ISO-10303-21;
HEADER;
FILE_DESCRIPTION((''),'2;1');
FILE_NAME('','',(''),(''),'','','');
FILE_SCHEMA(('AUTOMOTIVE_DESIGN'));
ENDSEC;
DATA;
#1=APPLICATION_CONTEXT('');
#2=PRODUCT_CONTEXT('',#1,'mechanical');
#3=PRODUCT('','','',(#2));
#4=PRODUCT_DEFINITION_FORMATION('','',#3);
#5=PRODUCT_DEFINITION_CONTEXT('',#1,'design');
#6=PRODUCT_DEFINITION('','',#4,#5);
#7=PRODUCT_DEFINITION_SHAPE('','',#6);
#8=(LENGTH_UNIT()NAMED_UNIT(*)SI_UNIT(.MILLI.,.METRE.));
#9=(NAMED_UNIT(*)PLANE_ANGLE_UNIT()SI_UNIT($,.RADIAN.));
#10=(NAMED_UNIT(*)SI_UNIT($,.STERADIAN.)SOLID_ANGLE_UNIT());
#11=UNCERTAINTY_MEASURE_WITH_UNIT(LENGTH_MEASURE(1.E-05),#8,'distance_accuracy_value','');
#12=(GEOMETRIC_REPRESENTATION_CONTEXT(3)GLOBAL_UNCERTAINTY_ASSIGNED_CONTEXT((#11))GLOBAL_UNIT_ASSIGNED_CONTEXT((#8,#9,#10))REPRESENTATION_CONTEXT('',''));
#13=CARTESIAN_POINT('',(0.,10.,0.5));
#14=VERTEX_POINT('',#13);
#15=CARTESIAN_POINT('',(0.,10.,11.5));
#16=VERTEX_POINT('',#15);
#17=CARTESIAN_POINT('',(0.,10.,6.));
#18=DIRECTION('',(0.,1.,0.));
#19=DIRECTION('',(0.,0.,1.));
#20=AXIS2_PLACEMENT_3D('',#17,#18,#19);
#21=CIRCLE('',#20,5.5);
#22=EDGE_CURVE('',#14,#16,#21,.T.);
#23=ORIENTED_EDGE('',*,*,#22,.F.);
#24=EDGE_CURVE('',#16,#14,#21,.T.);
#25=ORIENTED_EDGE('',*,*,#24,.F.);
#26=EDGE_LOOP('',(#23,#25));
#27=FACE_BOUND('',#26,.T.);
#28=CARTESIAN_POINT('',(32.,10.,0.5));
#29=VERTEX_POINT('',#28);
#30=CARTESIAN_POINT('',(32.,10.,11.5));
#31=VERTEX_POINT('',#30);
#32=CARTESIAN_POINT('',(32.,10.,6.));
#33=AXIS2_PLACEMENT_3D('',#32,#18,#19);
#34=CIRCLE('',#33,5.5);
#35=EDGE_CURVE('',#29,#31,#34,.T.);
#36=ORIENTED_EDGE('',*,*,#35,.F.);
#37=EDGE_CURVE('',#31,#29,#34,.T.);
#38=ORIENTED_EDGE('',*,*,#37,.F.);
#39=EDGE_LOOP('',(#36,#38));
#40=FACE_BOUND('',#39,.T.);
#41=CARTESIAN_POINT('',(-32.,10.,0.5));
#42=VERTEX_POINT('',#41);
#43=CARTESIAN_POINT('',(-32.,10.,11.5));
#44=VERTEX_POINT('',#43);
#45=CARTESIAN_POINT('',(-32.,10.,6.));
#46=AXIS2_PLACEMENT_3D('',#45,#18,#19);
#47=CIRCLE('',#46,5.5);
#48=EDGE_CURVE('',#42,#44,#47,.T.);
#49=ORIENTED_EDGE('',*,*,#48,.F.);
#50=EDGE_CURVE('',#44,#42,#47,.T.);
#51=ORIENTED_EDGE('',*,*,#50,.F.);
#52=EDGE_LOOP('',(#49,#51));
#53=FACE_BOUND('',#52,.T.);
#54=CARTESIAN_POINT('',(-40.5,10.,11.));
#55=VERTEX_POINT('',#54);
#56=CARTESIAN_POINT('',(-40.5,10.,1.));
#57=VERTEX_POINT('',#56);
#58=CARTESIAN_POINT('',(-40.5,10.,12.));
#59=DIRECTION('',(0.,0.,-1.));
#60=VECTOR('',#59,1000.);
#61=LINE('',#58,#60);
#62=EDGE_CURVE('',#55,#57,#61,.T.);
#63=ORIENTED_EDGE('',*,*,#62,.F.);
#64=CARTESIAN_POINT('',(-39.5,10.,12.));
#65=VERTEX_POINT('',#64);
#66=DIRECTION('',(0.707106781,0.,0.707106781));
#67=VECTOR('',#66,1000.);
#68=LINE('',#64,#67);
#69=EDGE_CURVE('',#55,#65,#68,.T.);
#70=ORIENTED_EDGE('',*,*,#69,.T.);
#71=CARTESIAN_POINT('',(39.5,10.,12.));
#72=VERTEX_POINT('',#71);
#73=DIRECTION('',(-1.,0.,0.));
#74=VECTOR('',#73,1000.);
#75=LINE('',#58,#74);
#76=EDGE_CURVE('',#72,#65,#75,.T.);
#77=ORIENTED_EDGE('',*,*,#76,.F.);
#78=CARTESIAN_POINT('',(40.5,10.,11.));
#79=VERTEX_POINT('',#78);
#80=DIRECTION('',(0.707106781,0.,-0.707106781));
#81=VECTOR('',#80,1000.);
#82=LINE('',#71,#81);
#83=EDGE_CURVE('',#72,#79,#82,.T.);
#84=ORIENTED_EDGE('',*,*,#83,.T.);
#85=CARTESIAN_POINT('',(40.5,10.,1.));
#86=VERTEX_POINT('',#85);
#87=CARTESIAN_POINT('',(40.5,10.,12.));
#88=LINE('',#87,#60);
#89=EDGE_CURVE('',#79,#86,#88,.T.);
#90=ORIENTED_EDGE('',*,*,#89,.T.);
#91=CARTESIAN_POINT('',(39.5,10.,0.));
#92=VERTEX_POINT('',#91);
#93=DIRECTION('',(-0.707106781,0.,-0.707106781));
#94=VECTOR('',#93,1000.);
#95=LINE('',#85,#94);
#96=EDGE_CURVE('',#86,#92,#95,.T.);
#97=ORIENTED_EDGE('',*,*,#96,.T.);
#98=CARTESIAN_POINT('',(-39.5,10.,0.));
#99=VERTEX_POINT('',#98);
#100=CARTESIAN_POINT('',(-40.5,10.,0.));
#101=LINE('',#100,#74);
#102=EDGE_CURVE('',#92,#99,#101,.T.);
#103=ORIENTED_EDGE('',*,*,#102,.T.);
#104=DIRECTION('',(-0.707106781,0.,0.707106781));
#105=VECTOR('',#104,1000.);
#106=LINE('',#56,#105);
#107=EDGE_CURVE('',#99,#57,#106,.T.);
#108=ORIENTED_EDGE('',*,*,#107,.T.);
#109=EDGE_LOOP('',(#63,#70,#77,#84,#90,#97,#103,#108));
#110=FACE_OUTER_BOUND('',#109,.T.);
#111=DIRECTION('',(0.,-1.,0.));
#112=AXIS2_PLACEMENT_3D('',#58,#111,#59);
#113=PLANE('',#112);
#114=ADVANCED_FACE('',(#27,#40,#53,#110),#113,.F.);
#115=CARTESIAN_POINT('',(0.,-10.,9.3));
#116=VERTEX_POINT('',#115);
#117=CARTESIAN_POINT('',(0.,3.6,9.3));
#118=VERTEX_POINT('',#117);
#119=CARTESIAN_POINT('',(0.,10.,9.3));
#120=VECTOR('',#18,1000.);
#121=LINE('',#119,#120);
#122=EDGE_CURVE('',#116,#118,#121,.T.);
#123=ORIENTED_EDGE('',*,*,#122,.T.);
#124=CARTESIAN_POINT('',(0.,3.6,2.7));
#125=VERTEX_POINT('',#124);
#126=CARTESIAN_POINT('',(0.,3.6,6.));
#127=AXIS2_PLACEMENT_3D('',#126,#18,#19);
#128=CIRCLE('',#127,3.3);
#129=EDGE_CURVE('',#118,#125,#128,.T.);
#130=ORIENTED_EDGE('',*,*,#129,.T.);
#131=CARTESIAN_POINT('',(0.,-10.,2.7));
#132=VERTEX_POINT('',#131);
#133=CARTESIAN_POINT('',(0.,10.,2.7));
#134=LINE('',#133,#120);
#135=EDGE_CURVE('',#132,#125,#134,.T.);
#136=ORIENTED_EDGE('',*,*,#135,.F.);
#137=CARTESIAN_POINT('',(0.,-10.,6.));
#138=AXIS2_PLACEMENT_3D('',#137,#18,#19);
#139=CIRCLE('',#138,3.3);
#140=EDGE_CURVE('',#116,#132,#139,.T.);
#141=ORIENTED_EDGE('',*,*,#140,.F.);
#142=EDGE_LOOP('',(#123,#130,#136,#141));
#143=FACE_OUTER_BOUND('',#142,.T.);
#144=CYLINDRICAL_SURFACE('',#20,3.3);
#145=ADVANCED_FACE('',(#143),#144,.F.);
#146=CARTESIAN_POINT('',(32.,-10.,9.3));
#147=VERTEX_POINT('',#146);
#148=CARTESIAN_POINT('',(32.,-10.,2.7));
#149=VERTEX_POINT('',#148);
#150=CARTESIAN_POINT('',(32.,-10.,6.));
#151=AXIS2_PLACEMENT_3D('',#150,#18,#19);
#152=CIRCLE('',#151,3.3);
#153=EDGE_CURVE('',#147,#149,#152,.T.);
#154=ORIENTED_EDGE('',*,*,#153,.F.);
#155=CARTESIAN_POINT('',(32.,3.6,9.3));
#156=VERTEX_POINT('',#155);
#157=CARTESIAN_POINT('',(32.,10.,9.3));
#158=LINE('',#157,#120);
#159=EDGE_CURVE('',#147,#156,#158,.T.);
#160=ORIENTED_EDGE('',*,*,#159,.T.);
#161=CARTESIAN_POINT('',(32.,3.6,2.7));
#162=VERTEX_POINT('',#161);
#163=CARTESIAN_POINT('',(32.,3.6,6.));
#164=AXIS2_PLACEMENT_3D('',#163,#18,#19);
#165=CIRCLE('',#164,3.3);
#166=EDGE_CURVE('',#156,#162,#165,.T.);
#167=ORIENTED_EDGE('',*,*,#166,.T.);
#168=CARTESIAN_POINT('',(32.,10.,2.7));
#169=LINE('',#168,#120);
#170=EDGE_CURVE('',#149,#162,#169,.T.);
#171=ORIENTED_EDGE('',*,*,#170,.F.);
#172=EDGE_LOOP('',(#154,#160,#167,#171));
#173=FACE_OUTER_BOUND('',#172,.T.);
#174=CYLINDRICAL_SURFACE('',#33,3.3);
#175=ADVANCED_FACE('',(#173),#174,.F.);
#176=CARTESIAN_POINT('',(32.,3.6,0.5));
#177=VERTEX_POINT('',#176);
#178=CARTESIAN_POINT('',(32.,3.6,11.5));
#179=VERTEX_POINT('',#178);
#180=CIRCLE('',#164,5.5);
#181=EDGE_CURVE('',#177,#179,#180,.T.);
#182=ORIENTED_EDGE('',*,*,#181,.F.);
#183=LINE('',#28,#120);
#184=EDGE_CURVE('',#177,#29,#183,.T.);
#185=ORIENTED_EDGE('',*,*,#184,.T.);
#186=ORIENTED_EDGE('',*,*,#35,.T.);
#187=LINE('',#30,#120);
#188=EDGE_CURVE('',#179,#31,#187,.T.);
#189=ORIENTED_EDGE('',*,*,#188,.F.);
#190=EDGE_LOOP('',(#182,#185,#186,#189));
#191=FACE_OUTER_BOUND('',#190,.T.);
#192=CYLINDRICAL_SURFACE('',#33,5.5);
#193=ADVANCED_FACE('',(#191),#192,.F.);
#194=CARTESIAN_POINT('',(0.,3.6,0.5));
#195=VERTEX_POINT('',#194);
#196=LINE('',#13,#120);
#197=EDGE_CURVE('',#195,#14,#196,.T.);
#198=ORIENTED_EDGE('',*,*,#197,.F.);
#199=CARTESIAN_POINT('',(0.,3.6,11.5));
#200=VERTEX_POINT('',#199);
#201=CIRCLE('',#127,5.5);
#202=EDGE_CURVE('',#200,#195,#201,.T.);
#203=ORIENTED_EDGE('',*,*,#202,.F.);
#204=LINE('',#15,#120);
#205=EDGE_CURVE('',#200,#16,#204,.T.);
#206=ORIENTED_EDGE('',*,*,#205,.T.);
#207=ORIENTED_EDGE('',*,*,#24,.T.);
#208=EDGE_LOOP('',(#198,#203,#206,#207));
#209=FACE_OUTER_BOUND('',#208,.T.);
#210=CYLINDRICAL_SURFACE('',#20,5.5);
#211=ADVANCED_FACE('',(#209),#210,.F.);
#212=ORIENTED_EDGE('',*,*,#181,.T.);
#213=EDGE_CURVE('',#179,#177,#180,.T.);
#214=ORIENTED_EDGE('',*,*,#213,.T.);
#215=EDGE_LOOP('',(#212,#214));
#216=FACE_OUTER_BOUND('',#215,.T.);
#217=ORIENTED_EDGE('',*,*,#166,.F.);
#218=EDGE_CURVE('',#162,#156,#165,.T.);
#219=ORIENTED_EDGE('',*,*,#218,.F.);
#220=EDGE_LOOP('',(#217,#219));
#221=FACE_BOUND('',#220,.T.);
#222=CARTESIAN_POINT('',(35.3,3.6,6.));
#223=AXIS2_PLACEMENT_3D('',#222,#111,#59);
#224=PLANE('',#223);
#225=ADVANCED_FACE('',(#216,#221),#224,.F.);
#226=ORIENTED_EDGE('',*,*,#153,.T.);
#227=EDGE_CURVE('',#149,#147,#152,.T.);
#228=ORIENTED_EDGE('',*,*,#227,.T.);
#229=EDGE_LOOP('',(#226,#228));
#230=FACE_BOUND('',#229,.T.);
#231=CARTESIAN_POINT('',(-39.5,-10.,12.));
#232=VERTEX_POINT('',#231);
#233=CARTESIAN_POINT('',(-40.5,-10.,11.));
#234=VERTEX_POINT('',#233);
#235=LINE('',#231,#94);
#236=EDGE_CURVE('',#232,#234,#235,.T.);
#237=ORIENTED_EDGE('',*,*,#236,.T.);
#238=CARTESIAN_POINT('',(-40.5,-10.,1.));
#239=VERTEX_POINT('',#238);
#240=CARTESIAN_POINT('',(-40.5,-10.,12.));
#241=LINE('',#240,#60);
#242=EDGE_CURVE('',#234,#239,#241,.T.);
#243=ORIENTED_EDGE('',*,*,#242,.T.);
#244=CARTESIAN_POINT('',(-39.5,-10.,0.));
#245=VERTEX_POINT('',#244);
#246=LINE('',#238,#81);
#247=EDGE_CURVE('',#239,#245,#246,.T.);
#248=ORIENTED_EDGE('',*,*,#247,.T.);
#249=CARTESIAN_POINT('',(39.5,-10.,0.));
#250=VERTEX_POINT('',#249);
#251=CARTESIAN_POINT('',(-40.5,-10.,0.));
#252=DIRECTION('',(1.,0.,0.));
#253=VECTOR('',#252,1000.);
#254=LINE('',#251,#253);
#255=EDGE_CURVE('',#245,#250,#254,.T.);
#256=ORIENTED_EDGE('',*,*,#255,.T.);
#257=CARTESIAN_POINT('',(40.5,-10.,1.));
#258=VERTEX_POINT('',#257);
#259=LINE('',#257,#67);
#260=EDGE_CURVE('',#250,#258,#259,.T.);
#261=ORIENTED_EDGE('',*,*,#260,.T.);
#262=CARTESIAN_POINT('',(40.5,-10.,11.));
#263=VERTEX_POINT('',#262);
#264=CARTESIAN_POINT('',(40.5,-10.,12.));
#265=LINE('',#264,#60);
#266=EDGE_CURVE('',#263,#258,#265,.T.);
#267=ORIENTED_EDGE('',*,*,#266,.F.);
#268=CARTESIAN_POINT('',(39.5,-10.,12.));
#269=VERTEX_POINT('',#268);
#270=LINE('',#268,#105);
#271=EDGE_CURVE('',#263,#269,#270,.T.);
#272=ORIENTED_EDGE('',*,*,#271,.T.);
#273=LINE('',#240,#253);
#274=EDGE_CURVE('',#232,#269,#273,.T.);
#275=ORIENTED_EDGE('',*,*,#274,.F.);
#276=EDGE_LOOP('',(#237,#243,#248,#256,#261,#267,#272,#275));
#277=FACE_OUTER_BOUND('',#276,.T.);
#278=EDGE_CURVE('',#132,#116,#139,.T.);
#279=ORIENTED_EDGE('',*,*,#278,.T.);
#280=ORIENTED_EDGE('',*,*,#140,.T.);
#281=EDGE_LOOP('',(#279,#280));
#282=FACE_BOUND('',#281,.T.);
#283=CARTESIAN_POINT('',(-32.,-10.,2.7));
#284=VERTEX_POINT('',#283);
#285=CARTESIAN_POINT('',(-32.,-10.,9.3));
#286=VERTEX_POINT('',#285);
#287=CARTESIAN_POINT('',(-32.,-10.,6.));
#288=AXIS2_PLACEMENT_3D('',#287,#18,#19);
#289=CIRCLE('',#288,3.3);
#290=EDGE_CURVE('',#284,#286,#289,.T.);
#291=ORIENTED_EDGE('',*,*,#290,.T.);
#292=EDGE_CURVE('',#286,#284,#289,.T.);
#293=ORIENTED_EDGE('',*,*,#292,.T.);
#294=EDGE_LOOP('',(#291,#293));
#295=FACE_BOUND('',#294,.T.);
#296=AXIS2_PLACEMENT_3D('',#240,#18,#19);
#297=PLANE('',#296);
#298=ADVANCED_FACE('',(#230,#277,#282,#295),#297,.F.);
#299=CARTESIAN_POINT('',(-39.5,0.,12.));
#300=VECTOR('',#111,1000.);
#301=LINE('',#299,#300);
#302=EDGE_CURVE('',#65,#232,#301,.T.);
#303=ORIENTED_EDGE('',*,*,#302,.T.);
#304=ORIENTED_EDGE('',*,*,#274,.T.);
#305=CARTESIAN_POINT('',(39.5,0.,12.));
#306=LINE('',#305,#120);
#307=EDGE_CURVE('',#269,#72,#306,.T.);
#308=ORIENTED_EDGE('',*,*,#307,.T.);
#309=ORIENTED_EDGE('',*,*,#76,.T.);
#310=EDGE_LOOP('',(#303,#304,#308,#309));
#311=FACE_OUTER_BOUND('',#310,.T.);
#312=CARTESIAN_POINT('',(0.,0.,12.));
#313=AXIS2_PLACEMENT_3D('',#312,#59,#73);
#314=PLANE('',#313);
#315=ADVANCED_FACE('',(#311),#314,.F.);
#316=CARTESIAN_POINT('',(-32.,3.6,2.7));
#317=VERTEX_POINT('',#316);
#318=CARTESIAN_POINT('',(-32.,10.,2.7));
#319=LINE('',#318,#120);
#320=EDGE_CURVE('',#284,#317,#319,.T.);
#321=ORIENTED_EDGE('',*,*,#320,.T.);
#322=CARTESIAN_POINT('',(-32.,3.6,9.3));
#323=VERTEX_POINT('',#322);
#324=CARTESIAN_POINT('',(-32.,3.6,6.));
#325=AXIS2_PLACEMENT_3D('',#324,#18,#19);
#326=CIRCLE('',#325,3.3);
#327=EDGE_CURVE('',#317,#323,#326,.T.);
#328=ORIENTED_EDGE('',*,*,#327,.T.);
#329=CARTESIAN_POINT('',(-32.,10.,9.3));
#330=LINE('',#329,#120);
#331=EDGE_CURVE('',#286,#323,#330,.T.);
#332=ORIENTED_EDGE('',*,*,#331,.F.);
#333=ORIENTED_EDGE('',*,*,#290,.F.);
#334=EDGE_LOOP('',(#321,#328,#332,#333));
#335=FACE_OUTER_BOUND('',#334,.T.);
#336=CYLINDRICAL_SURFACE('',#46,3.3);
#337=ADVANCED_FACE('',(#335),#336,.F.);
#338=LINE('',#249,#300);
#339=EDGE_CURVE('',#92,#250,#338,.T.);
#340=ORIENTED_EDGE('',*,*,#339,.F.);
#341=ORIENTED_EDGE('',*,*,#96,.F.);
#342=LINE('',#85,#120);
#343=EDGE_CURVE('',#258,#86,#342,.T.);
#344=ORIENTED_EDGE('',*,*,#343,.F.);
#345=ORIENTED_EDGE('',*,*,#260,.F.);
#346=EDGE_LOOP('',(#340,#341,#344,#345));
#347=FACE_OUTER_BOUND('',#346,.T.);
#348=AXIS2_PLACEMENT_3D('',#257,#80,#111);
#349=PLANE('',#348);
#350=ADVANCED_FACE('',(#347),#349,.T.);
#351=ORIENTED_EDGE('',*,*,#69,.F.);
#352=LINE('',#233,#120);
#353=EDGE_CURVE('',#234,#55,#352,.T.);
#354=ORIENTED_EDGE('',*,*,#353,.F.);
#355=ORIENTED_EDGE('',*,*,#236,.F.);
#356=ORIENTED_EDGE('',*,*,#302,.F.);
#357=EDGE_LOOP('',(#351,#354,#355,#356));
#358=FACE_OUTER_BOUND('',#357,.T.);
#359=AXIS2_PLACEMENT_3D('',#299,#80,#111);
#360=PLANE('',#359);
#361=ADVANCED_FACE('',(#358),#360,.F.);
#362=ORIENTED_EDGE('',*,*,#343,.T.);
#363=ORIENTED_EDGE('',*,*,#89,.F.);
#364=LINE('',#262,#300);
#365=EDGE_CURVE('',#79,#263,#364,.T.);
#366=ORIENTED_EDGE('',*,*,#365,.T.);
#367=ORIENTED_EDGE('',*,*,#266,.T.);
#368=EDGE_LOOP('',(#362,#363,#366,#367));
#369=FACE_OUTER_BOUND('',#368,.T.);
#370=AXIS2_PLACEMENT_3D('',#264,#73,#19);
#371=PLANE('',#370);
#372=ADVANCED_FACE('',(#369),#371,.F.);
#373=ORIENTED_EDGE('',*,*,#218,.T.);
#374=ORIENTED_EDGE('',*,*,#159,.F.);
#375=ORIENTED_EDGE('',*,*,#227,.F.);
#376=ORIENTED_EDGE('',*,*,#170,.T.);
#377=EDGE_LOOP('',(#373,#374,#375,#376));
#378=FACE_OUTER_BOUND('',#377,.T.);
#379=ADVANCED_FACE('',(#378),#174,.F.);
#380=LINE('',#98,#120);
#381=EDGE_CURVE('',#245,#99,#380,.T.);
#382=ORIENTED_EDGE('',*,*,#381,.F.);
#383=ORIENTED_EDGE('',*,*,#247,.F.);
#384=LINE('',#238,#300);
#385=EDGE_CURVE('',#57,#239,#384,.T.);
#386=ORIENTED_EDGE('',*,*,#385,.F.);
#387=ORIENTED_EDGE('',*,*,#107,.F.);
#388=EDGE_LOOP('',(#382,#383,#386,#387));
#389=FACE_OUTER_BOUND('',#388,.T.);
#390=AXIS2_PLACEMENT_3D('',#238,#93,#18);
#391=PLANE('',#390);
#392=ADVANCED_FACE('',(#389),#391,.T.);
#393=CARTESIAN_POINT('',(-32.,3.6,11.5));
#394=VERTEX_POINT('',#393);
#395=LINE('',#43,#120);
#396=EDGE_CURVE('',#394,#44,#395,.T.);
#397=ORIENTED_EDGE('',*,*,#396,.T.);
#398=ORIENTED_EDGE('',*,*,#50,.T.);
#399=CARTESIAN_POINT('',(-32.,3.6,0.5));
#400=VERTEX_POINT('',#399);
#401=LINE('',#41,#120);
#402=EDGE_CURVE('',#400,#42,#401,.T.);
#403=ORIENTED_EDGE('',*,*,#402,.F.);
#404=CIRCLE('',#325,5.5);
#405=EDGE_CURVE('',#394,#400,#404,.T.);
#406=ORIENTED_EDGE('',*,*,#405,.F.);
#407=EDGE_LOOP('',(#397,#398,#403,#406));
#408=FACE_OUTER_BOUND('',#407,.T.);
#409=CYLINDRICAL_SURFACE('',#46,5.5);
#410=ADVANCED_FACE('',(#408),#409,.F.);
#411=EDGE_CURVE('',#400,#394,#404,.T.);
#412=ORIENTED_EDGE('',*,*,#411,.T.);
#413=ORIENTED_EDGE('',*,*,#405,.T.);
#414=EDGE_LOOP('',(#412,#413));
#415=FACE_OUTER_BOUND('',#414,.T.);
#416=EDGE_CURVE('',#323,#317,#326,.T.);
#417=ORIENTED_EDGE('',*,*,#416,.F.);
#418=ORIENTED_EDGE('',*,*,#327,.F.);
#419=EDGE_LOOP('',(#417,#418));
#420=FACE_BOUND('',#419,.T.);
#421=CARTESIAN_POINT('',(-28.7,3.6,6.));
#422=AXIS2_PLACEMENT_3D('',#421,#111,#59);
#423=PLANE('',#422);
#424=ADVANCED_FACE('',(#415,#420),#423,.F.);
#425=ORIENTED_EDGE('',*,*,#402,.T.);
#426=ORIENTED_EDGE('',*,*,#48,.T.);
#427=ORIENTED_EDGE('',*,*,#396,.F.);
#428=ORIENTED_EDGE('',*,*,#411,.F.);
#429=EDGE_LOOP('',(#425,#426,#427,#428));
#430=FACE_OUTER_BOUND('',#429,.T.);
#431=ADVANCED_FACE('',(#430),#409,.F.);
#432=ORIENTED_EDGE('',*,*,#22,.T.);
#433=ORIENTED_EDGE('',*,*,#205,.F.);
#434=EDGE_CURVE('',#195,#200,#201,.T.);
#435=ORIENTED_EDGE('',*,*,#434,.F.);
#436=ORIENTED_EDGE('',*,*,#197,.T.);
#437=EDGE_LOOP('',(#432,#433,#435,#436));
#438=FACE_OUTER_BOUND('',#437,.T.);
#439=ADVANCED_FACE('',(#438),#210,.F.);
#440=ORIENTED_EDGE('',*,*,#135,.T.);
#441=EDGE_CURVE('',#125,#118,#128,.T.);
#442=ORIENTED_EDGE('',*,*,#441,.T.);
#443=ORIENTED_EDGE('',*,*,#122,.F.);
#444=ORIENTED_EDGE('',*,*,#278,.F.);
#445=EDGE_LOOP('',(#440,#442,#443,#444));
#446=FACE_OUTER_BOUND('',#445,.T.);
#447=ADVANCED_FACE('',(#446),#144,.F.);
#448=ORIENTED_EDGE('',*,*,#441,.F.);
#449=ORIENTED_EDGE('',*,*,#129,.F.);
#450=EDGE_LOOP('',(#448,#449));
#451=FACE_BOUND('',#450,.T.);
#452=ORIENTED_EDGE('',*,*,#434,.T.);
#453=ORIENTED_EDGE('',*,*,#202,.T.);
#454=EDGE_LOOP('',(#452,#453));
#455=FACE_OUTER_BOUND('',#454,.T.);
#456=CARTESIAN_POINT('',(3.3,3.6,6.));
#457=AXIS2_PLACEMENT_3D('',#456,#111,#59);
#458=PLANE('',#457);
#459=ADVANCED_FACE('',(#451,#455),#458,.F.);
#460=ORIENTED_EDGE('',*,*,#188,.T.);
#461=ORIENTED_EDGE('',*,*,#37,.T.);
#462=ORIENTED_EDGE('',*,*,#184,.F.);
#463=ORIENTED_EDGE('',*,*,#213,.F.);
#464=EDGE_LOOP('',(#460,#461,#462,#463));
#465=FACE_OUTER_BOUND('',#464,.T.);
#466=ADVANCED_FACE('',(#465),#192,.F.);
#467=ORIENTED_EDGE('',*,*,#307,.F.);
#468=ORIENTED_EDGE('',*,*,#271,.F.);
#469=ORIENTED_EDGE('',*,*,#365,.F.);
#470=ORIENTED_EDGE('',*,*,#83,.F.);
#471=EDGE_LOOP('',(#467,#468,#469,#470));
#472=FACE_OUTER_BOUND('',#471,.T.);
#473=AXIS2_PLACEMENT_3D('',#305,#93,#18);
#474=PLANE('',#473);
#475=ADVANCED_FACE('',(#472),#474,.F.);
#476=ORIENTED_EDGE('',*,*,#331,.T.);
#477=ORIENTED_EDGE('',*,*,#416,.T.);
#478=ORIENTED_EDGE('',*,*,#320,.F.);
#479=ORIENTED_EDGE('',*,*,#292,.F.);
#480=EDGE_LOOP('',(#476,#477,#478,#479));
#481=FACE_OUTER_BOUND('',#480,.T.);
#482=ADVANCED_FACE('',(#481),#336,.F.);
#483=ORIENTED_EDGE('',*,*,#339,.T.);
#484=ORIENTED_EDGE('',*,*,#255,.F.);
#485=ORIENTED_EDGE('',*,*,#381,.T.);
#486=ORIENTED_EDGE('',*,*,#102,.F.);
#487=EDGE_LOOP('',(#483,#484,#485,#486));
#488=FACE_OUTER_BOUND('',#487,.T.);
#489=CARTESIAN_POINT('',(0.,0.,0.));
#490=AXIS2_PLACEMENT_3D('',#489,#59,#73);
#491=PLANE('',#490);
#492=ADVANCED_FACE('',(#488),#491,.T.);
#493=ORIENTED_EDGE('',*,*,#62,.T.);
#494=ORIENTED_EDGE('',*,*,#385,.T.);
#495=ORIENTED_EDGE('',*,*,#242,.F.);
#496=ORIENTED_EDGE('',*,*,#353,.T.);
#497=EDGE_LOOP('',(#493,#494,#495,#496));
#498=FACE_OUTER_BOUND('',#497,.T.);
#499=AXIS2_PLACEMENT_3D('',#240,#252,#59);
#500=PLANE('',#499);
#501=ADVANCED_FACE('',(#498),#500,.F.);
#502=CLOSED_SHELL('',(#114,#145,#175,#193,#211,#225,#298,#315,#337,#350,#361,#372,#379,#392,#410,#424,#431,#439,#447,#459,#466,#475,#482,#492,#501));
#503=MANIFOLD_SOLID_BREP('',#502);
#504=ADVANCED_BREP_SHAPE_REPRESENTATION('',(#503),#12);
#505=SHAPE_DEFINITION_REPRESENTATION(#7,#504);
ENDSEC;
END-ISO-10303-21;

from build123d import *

# Parameters (mm, degrees)
SKETCH_1_W                   = 81
SKETCH_1_H                   = 20
EXTRUDE_1_DEPTH              = 12
HOLE_WIZARD_M6_1_D           = 6.6
HOLE_WIZARD_M6_1_CBORE_D     = 11
HOLE_WIZARD_M6_1_CBORE_DEPTH = 6.4
CHAMFER_1_SIZE               = 1


with BuildPart() as part:
    # 草图1 → 凸台-拉伸1 (new body)
    with BuildSketch(Plane.XY):
        Rectangle(SKETCH_1_W, SKETCH_1_H)
    extrude(amount=EXTRUDE_1_DEPTH)

    # M6 六角凹头螺钉的柱形沉头孔1 (through all)
    with Locations(Plane(origin=(0, 10, 0), x_dir=(1, 0, 0), z_dir=(0, 1, 0))):
        with Locations((-32, -6), (0, -6), (32, -6)):
            CounterBoreHole(HOLE_WIZARD_M6_1_D / 2, HOLE_WIZARD_M6_1_CBORE_D / 2, HOLE_WIZARD_M6_1_CBORE_DEPTH)

    # 倒角1
    chamfer_1_edges = [part.edges().sort_by_distance(p)[0] for p in [
        (-40.5, 0, 12),
        (40.5, 0, 12),
        (-40.5, 0, 0),
        (40.5, 0, 0),
    ]]
    chamfer(chamfer_1_edges, length=CHAMFER_1_SIZE)


solid = part.part
